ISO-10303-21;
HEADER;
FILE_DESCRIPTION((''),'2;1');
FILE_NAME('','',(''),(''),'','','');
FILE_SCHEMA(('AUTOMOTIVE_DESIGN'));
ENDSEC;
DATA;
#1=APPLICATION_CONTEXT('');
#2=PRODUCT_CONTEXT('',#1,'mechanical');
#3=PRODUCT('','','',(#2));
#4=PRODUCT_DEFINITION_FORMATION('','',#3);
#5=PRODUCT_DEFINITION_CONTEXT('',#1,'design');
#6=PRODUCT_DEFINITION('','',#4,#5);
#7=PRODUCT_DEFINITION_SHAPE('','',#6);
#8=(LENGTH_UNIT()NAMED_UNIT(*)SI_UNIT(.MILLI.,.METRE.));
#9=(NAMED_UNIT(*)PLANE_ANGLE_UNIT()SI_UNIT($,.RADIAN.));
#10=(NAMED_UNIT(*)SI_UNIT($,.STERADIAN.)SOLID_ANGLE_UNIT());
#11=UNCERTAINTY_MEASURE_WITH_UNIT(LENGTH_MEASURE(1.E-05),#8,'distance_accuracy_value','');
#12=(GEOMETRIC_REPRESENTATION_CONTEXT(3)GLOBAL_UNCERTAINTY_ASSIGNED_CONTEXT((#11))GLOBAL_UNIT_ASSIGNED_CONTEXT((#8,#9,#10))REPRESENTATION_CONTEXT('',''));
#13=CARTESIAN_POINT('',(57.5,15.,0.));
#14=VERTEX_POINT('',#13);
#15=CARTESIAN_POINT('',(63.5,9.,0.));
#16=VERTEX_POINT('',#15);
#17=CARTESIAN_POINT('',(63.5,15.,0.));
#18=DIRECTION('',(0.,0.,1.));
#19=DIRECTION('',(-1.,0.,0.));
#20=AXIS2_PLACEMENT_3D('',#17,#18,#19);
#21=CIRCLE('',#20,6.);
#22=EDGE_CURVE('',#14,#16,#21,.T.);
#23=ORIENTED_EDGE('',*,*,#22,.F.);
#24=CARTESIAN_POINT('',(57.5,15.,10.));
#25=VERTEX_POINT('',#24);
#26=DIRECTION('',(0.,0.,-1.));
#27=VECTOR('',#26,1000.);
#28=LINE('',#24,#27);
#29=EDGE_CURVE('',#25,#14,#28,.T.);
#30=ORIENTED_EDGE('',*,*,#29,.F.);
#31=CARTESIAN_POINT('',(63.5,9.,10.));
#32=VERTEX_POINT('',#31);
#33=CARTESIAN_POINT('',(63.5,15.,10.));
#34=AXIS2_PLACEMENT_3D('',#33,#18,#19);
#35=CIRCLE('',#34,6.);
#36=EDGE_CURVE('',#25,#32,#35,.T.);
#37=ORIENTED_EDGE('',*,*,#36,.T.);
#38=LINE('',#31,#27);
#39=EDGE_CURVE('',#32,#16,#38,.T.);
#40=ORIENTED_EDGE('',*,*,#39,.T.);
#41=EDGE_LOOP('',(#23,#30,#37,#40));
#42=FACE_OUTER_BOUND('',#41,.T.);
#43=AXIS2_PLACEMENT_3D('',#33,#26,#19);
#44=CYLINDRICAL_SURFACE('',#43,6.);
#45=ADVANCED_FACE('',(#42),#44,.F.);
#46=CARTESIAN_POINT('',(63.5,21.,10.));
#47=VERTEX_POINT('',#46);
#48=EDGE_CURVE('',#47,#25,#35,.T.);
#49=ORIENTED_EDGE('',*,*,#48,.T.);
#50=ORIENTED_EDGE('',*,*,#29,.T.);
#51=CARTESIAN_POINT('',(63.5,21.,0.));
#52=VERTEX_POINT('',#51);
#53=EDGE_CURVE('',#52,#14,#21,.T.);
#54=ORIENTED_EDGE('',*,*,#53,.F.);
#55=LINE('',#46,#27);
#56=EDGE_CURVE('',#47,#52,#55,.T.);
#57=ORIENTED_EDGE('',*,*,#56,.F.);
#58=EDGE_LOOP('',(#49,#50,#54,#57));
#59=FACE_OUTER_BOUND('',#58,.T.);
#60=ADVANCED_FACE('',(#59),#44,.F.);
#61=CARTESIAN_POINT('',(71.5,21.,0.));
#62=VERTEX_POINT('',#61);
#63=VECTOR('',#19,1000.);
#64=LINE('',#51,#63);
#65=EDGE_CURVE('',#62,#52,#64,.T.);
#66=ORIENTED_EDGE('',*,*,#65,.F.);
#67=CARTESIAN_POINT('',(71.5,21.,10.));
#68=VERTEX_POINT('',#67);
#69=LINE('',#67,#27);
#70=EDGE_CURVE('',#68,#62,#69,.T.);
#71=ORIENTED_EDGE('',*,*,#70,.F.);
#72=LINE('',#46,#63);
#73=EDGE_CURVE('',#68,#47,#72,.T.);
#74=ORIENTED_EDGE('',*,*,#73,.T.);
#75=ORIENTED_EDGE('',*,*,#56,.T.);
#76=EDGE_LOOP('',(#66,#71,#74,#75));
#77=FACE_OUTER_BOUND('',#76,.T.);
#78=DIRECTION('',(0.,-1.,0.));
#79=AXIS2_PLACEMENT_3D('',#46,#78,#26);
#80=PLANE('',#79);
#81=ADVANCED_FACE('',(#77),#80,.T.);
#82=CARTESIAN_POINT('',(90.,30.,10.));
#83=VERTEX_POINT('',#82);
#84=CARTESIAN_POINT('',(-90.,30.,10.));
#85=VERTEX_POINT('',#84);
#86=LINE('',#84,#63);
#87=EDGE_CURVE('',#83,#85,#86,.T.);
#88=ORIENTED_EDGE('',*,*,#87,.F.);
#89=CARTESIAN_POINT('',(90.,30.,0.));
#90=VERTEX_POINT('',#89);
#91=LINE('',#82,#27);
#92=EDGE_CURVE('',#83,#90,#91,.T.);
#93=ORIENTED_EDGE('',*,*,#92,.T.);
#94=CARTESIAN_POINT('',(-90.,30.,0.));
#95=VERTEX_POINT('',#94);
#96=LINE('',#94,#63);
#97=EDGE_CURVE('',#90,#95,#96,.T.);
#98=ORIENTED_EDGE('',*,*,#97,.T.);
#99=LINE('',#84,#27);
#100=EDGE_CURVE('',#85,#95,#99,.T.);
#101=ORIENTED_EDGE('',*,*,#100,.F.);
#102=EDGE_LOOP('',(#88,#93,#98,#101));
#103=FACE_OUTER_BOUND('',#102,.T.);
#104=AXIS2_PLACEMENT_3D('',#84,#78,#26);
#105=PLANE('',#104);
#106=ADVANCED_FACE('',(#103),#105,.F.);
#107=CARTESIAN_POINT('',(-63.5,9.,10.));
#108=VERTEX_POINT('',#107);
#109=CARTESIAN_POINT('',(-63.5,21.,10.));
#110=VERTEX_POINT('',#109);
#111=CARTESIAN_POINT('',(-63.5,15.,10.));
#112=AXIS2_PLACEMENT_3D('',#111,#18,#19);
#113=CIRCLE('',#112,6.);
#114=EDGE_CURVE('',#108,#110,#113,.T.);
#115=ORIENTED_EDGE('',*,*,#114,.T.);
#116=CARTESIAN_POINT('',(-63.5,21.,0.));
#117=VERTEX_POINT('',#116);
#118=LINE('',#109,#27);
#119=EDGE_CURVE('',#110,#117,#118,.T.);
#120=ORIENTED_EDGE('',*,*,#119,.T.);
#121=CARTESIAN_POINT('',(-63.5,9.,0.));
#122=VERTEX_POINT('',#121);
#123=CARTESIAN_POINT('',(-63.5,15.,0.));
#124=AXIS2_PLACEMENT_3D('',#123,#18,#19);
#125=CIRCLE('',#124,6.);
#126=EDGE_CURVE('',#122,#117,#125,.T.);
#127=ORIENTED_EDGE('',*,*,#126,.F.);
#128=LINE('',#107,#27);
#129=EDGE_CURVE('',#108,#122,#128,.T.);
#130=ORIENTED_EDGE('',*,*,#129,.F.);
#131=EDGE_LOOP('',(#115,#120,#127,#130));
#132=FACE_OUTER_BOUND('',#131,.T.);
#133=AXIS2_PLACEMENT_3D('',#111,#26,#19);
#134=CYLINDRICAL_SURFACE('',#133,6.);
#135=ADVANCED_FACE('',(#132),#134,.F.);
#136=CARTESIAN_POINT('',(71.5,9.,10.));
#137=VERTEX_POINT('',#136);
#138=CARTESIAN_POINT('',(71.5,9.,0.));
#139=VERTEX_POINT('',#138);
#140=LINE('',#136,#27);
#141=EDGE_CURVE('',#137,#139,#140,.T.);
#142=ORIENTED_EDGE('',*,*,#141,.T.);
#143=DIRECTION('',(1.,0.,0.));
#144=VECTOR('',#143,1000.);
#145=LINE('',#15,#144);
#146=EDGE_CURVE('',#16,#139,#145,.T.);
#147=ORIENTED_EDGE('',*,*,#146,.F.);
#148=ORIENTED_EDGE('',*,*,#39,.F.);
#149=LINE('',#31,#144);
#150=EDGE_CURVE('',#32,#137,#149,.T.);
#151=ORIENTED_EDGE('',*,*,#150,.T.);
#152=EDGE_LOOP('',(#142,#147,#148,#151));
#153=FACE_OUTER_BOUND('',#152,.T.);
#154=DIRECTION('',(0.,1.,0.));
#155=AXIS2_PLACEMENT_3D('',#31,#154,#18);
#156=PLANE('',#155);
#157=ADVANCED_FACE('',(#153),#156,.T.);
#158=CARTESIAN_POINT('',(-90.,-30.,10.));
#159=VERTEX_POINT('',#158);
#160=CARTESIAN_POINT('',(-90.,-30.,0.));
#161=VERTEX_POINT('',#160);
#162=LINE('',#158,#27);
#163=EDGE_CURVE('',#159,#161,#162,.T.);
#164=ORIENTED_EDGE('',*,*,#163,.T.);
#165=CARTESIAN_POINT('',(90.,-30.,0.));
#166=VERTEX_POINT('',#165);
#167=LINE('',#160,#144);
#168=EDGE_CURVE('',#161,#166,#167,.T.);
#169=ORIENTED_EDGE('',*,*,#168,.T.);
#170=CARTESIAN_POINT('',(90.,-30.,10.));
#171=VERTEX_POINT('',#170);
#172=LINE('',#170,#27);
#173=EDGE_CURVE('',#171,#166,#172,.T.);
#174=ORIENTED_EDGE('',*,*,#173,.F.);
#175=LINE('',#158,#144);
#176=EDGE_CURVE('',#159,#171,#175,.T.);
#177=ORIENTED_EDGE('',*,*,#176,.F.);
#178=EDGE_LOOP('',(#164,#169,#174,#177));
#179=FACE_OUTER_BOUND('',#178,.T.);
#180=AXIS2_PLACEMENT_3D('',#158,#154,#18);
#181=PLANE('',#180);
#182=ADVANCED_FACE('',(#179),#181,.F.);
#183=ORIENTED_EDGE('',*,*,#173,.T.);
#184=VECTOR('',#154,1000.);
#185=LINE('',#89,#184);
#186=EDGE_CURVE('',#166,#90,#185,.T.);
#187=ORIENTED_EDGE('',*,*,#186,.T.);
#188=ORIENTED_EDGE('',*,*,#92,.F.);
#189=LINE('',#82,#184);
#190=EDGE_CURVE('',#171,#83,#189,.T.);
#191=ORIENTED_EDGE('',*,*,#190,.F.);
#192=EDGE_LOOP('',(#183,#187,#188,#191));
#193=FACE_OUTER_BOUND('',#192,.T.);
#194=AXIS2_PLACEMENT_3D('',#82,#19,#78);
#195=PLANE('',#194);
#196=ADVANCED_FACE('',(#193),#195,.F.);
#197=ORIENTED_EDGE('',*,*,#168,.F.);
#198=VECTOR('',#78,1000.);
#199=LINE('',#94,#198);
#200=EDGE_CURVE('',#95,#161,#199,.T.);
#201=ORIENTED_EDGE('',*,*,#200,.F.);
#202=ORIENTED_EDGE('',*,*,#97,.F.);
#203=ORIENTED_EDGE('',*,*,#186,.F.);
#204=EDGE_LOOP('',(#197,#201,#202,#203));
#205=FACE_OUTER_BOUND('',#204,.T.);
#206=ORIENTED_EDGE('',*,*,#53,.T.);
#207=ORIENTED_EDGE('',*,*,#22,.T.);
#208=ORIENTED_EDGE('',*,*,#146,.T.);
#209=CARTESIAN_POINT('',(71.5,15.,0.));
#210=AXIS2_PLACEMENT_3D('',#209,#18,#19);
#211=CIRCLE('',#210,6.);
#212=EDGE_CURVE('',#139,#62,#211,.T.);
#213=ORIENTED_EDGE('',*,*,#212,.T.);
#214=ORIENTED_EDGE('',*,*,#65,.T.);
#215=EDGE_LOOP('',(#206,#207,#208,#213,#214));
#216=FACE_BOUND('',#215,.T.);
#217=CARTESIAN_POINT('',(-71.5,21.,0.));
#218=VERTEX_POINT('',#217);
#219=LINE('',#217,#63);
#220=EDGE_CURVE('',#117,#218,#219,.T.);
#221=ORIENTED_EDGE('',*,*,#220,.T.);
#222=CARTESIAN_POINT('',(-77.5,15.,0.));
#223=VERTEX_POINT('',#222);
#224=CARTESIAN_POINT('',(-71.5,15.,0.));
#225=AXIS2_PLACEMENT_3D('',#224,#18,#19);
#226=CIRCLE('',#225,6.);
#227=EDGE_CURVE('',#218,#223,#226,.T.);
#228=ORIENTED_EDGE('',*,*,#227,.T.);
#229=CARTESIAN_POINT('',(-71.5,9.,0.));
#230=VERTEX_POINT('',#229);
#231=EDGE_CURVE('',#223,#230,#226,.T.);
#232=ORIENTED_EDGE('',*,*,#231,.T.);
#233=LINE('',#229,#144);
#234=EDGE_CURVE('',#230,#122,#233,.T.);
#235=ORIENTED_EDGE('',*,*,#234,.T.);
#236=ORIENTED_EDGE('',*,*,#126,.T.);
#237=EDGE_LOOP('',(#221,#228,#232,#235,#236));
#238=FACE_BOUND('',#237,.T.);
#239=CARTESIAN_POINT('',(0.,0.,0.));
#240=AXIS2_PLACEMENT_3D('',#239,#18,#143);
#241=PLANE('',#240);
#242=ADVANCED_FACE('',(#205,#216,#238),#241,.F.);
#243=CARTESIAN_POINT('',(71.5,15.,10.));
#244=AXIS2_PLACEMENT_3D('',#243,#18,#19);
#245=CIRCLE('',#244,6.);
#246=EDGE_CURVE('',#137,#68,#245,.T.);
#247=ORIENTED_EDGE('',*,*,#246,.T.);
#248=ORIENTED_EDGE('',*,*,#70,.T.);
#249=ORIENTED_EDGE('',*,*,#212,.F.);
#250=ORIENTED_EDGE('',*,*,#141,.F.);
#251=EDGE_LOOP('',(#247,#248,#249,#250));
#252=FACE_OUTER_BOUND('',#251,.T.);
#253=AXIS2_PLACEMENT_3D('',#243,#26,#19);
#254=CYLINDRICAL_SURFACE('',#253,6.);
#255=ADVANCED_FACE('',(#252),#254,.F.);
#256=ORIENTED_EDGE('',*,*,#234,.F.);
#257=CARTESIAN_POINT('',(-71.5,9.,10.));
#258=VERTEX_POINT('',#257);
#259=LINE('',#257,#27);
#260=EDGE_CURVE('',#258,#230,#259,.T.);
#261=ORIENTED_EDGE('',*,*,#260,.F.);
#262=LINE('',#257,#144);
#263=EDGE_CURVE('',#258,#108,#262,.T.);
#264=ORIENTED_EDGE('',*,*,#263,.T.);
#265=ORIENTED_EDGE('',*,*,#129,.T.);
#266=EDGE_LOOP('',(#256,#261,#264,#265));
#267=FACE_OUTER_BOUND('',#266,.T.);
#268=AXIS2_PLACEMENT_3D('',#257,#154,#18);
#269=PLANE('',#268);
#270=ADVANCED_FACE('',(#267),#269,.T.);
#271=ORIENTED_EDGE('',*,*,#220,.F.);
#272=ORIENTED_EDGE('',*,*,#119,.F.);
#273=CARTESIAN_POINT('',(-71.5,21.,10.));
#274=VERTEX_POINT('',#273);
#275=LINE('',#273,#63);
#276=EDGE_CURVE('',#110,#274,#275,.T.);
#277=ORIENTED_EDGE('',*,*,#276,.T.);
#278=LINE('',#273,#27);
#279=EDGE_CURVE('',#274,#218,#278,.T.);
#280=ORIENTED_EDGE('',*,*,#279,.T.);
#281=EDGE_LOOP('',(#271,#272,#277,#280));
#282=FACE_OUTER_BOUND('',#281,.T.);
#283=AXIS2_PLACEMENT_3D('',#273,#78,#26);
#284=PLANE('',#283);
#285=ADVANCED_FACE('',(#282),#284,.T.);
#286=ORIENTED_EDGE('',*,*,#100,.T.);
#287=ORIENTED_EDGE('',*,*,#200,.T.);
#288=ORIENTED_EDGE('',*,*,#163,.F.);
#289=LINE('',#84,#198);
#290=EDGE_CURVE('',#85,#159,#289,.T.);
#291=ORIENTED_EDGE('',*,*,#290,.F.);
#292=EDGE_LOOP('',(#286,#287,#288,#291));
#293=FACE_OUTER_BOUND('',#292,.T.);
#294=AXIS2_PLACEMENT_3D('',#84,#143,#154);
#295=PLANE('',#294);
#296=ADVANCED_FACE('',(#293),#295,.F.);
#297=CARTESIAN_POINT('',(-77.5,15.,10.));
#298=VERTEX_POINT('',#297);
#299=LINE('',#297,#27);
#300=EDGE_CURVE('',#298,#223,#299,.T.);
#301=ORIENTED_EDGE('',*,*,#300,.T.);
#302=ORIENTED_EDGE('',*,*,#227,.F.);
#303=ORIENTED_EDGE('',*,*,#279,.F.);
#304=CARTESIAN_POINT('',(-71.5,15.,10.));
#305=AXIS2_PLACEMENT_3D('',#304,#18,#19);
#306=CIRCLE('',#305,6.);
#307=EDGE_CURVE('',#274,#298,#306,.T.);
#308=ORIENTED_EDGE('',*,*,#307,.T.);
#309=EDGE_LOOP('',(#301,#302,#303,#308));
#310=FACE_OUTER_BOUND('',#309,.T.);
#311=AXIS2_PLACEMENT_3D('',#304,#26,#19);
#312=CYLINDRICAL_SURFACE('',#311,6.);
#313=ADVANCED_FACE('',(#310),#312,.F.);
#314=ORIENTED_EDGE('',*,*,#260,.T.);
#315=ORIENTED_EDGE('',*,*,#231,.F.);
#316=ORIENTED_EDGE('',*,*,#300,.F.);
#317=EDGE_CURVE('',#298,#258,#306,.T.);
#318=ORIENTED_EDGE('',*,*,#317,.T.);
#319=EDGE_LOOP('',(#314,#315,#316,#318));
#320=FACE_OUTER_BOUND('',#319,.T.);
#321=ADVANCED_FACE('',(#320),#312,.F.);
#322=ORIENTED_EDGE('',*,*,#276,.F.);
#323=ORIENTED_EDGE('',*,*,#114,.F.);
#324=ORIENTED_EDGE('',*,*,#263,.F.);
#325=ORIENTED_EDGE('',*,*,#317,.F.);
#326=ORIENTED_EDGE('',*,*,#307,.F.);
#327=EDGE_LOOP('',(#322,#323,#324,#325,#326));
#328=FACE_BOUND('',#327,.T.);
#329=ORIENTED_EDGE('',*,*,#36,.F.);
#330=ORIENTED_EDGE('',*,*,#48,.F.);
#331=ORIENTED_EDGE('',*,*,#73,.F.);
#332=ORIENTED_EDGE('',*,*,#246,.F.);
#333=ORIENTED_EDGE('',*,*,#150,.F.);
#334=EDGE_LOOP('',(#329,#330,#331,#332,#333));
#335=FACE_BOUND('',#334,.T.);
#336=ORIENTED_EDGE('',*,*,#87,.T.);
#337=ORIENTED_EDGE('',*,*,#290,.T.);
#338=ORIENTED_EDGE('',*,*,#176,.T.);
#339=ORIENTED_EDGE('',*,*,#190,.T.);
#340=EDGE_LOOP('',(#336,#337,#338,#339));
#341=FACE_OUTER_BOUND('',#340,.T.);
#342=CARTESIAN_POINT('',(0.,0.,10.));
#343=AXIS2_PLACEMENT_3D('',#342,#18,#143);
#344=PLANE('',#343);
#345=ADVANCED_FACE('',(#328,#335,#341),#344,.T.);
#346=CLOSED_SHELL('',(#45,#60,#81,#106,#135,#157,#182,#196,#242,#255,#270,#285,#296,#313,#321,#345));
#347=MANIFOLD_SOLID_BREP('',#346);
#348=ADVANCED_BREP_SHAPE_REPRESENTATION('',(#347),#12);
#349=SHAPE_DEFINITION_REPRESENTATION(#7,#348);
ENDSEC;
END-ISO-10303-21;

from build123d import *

# Parameters (mm, degrees)
SKETCH_1_W      = 180
SKETCH_1_H      = 60
EXTRUDE_1_DEPTH = 10


with BuildPart() as part:
    # 草图1 → 凸台-拉伸1 (new body)
    with BuildSketch(Plane.XY):
        Rectangle(SKETCH_1_W, SKETCH_1_H)
        with BuildLine():
            Line((-71.5, 21), (-63.5, 21))
            ThreePointArc((-63.5, 21), (-57.5, 15), (-63.5, 9))
            Line((-63.5, 9), (-71.5, 9))
            ThreePointArc((-71.5, 9), (-77.5, 15), (-71.5, 21))
        make_face(mode=Mode.SUBTRACT)
        with BuildLine():
            Line((63.5, 21), (71.5, 21))
            ThreePointArc((71.5, 21), (77.5, 15), (71.5, 9))
            Line((71.5, 9), (63.5, 9))
            ThreePointArc((63.5, 9), (57.5, 15), (63.5, 21))
        make_face(mode=Mode.SUBTRACT)
    extrude(amount=EXTRUDE_1_DEPTH)


solid = part.part
